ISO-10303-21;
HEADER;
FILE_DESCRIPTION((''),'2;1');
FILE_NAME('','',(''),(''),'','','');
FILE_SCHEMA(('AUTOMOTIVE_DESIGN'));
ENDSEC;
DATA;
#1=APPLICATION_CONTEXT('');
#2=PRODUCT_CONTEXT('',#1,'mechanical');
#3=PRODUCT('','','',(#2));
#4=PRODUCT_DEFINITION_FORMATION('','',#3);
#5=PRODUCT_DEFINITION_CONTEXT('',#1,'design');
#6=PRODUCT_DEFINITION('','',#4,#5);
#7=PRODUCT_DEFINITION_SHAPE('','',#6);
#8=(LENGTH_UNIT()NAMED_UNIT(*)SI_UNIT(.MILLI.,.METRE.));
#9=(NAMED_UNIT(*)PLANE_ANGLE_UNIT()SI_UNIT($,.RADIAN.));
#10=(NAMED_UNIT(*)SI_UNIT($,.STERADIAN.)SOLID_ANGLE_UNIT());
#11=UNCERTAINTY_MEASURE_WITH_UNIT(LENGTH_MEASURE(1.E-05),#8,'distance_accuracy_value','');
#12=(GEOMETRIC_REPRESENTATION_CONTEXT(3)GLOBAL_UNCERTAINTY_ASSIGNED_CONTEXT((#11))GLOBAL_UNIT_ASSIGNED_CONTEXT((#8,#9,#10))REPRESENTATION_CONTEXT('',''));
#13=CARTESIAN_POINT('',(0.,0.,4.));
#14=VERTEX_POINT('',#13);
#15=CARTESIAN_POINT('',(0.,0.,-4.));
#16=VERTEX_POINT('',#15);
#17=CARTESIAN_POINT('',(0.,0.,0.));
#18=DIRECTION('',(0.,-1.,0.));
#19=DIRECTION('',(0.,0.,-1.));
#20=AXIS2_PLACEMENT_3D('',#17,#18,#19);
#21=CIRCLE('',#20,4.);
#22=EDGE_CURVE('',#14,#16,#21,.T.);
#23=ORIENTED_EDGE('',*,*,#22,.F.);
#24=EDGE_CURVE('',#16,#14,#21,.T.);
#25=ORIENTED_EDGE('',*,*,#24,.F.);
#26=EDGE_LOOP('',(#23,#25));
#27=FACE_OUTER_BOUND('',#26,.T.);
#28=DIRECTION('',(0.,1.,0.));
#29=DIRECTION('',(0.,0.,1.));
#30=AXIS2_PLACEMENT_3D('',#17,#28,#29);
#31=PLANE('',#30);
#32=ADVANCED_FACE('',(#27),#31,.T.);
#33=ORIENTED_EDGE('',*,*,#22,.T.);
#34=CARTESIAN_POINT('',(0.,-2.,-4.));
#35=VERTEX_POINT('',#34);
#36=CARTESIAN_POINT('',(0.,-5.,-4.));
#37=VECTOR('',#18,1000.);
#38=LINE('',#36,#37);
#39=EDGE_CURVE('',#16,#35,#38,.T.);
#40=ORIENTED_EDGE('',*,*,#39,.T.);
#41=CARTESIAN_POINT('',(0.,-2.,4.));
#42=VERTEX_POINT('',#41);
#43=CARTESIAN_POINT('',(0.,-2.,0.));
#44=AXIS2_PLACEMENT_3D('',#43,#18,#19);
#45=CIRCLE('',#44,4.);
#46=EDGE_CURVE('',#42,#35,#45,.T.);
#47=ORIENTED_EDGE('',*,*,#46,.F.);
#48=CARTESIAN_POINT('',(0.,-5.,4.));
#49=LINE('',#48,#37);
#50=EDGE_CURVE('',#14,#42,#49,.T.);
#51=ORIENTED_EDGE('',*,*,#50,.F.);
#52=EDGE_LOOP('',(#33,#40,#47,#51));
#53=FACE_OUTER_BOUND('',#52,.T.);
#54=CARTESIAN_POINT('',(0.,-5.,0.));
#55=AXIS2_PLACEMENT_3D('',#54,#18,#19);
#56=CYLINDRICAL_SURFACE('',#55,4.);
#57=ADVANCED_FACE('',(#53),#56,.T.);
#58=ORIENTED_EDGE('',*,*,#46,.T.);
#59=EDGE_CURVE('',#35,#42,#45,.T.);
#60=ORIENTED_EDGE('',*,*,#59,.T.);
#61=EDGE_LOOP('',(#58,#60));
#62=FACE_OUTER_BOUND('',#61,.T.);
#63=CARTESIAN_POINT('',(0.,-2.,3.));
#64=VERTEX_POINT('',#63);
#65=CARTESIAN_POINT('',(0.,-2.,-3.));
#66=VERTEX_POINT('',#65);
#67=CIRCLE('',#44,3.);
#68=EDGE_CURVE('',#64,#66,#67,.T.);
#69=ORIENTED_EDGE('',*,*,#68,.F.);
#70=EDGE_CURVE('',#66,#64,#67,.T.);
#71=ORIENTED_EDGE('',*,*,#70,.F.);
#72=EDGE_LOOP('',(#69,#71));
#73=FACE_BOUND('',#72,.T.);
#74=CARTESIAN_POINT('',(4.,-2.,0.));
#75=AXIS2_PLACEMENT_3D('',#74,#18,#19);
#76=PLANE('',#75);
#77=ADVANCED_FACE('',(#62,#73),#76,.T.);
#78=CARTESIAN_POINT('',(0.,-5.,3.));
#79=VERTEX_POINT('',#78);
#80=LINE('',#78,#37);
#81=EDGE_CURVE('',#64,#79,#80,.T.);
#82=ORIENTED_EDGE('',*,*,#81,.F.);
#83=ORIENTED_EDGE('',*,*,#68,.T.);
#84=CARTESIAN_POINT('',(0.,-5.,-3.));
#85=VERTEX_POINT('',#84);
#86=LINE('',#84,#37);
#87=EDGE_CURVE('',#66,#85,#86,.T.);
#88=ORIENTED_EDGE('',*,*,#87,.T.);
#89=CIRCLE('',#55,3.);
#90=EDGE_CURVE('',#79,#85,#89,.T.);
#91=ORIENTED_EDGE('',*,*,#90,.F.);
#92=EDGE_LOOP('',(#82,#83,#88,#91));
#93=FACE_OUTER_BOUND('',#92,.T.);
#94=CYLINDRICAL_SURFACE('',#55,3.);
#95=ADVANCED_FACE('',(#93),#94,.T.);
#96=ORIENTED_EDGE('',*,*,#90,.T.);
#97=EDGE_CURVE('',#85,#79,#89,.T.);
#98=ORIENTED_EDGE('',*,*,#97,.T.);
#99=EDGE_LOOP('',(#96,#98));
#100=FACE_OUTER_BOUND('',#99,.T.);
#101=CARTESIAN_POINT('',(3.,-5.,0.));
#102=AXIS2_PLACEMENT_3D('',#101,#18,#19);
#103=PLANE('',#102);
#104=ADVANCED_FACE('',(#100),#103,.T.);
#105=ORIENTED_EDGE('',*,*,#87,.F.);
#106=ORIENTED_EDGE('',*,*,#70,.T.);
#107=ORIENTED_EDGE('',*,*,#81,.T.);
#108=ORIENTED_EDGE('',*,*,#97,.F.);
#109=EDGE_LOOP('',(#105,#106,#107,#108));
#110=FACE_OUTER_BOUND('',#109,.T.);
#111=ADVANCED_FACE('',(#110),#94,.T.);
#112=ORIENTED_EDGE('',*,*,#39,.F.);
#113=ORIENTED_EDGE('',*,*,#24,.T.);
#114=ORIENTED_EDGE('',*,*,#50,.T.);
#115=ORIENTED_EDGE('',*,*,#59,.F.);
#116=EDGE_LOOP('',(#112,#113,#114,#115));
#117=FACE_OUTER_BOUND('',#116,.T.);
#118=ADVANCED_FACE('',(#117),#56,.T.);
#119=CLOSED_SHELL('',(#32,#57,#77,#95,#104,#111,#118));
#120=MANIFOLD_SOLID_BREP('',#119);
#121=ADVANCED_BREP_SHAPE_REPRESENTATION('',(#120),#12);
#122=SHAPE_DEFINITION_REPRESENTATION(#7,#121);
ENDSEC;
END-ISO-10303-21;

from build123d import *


with BuildPart() as part:
    # Sketch1 → Revolve1 (revolve)
    with BuildSketch(Plane.XY, mode=Mode.PRIVATE) as revolve1_sk:
        Polygon((0, 0), (4, 0), (4, -2), (3, -2), (3, -5), (0, -5), align=None)
    revolve(revolve1_sk.sketch.rotate(Axis((0, -5, 0), (0, 1, 0)), 90), axis=Axis((0, -5, 0), (0, 1, 0)))


solid = part.part
